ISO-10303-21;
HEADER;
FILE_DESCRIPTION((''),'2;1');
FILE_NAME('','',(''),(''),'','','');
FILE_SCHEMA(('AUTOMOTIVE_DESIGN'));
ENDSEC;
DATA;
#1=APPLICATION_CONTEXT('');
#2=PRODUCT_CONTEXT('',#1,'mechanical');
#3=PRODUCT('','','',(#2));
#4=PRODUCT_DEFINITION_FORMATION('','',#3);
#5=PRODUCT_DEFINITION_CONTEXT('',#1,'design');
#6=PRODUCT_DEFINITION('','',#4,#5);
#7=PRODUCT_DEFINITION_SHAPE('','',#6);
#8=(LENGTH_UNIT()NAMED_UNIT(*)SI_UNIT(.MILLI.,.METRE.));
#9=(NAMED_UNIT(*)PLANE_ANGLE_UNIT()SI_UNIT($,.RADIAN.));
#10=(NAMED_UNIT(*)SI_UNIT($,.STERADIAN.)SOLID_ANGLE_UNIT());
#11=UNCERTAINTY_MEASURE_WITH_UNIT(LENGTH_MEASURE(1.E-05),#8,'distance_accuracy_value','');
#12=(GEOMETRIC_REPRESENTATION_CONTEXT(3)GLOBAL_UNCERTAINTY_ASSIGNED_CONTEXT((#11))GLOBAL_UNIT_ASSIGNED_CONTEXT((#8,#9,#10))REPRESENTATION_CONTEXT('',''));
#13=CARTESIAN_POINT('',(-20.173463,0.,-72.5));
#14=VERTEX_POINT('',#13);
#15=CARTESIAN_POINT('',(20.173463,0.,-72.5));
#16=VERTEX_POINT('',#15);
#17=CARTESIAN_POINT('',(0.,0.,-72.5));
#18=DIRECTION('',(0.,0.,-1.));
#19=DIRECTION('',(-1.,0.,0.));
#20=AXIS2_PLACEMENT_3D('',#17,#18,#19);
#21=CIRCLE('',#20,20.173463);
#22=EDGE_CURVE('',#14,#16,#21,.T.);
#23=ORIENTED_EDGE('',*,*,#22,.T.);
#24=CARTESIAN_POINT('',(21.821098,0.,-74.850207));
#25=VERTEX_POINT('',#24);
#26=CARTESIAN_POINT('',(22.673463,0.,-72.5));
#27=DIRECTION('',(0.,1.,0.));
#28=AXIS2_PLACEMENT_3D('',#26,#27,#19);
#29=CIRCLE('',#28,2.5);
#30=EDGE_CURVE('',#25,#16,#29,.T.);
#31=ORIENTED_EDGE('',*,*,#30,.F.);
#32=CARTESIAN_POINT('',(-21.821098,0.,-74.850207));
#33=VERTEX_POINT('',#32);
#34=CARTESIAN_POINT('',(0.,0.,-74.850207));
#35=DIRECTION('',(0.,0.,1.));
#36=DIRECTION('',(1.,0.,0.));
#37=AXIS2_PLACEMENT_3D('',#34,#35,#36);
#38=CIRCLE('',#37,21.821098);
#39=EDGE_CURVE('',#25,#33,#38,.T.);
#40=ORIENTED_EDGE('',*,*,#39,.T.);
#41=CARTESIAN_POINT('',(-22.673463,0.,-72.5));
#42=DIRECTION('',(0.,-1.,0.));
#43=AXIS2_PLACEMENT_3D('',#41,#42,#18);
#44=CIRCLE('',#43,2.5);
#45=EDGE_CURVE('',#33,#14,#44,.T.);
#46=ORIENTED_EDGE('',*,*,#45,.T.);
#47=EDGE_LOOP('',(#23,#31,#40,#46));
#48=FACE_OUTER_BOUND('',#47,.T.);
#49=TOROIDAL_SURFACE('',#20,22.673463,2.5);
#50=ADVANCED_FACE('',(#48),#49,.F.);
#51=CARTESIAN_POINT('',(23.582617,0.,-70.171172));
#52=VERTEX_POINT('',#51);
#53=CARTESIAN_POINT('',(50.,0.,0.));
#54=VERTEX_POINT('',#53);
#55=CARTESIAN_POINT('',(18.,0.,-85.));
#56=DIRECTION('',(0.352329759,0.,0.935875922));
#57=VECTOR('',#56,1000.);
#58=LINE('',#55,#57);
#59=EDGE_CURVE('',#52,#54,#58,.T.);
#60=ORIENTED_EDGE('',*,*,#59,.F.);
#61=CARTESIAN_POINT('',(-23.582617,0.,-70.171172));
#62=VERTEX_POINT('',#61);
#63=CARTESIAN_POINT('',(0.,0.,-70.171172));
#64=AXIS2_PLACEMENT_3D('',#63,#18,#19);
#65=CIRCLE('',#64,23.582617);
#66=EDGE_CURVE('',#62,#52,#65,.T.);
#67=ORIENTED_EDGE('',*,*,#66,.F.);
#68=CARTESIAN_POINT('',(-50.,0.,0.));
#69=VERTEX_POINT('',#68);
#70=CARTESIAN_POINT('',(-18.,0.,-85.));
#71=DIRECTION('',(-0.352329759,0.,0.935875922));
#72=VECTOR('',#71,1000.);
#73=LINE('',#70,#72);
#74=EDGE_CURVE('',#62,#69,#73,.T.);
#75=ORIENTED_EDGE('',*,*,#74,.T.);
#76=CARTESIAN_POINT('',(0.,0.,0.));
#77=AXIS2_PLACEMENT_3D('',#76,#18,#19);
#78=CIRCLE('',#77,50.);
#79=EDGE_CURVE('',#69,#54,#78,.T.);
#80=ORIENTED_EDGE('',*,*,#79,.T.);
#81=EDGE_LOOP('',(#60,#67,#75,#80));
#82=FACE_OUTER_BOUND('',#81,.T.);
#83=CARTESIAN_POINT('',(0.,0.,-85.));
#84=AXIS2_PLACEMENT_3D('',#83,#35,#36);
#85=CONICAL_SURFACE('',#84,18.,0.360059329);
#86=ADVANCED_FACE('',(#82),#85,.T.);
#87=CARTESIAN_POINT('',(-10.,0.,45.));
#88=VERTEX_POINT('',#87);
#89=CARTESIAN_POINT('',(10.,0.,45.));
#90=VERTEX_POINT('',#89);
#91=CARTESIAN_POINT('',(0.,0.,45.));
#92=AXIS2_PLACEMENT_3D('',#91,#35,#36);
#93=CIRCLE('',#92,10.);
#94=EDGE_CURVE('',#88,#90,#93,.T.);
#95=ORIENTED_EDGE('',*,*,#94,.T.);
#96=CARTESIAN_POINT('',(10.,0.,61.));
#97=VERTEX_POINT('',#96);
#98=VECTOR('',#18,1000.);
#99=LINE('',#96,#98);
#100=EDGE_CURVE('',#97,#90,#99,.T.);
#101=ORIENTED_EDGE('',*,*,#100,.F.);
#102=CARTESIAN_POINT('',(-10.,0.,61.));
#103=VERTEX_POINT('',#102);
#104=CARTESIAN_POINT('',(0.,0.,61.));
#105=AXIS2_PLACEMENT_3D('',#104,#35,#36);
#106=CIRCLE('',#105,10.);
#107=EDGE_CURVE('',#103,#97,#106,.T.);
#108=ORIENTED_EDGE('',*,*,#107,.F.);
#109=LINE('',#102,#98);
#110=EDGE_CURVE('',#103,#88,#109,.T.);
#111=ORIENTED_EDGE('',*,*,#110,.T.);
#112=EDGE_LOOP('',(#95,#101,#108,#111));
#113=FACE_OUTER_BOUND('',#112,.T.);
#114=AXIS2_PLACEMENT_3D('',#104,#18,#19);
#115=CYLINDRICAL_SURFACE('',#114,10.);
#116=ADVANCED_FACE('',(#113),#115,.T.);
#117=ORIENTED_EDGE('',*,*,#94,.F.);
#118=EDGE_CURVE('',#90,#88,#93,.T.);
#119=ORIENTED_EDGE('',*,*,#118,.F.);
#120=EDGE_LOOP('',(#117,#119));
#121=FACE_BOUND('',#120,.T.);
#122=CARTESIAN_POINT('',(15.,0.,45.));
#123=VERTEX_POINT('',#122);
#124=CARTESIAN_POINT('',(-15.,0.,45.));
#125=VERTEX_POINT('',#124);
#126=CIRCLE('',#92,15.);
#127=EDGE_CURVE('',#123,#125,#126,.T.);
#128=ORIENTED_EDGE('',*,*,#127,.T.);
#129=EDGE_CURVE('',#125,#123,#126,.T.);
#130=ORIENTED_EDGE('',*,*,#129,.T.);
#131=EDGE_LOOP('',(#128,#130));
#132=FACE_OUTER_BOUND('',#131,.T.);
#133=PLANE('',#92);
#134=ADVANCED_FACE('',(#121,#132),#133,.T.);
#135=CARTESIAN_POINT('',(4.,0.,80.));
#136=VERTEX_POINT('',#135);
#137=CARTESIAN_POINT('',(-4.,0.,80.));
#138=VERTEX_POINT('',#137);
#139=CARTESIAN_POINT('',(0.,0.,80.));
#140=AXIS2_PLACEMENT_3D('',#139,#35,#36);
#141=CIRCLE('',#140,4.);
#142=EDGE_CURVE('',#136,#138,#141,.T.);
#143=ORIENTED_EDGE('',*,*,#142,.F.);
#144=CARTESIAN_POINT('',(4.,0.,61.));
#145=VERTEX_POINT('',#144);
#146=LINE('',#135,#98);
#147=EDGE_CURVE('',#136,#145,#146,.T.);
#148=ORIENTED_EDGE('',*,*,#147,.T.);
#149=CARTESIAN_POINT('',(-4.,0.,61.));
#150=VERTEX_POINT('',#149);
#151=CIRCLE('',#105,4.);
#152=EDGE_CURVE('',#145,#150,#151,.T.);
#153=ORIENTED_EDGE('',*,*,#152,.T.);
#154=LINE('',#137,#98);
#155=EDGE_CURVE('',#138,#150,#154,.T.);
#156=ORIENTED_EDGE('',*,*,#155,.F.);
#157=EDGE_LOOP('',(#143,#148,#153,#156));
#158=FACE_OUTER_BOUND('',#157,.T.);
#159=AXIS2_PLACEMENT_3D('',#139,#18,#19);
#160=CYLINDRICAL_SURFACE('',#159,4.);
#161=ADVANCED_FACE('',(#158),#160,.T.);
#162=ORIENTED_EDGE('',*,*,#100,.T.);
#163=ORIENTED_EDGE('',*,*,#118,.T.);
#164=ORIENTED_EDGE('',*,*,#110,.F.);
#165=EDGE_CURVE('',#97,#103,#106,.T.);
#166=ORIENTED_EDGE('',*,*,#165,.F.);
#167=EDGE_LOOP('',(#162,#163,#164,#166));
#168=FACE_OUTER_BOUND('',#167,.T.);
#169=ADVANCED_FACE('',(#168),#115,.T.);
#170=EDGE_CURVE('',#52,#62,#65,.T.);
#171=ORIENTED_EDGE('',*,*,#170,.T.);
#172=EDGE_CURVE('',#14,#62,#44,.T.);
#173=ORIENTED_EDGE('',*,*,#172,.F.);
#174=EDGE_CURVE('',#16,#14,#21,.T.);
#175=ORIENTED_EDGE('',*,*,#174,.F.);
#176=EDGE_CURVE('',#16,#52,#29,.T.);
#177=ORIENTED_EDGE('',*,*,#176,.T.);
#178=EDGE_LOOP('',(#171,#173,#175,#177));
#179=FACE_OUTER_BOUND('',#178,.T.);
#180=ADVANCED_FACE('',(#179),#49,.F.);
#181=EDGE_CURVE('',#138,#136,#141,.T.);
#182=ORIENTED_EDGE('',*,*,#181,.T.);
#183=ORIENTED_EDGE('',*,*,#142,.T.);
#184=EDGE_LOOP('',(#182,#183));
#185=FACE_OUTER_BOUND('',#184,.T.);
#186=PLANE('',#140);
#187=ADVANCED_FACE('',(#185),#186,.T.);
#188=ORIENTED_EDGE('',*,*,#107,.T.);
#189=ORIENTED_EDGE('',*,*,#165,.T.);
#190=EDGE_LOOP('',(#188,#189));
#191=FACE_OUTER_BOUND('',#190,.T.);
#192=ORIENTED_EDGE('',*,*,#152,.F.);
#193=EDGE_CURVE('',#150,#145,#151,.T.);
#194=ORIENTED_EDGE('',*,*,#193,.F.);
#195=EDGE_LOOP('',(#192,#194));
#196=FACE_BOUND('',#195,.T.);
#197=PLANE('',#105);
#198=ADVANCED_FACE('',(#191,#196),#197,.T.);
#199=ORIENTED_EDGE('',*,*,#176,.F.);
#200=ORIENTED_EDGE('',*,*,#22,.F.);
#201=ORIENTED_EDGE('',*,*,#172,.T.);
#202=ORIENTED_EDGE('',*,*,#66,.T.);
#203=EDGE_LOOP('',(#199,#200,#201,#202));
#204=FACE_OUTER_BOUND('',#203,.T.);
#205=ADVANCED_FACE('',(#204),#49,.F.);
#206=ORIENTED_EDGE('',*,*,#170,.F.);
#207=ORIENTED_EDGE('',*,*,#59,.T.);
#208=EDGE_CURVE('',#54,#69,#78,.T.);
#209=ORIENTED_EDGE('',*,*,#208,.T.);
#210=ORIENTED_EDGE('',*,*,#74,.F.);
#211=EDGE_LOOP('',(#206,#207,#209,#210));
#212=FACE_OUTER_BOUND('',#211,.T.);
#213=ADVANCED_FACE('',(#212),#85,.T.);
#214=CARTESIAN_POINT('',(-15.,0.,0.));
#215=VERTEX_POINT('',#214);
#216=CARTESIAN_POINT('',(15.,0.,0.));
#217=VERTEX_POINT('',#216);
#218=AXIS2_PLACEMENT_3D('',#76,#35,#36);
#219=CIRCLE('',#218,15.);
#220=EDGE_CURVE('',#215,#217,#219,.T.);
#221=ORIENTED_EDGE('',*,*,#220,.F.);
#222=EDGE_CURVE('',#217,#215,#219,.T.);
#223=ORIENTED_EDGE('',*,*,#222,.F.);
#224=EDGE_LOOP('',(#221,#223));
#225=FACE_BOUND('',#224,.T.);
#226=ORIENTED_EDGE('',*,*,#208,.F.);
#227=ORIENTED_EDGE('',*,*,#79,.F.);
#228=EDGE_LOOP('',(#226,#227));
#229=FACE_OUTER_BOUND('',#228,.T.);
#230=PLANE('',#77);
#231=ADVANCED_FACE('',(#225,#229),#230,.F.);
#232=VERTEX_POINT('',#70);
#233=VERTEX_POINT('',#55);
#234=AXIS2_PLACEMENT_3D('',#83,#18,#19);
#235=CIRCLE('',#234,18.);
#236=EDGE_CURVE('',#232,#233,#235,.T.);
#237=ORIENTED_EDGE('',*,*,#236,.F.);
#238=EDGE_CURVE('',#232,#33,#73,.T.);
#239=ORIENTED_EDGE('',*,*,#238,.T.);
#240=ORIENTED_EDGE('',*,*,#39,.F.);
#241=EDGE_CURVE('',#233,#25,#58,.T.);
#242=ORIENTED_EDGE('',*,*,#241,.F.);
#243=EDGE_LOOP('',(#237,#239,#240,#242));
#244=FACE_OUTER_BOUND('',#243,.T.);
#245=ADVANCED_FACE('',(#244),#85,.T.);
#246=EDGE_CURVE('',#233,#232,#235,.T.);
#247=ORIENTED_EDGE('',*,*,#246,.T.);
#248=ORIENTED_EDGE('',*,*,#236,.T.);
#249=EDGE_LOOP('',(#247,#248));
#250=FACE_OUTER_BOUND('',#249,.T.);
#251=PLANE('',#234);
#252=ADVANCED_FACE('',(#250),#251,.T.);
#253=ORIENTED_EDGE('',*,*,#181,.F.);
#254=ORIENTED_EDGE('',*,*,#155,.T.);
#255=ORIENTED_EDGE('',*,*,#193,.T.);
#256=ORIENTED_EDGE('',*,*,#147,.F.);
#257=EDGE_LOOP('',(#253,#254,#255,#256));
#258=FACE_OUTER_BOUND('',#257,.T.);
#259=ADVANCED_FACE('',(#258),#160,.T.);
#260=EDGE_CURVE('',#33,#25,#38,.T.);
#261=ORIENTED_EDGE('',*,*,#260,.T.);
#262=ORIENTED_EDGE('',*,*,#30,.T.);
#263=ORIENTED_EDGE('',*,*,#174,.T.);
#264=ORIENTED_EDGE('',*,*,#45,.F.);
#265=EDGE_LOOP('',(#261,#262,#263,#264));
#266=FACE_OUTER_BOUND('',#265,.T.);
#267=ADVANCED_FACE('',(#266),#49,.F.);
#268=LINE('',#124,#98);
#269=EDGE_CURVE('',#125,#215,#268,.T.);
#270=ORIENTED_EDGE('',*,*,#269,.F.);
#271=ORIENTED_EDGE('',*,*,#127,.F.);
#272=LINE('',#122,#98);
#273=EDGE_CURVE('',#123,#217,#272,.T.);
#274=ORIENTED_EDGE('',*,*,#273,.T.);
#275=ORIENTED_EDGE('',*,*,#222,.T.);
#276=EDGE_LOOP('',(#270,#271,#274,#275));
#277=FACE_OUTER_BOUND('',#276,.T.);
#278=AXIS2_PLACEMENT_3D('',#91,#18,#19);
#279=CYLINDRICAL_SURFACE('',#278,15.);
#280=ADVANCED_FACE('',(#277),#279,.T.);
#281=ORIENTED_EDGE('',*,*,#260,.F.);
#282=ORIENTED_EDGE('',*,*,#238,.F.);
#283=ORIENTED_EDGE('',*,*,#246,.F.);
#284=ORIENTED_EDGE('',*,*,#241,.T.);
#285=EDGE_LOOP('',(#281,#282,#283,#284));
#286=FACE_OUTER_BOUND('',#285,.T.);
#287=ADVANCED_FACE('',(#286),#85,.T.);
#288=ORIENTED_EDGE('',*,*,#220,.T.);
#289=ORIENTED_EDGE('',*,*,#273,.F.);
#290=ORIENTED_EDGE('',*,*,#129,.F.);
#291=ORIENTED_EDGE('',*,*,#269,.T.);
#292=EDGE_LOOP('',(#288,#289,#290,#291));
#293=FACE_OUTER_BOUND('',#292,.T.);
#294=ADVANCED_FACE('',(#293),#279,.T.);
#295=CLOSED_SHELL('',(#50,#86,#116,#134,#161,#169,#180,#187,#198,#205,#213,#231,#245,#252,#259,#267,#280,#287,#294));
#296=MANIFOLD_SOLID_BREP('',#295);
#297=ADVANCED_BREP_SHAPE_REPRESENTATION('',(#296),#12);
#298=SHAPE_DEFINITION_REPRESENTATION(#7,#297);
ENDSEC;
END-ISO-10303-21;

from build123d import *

# Parameters (mm, degrees)
SHAFT_BASE_30_SKETCH_R     = 15
SHAFT_BASE_30_DEPTH        = 45
SHAFT_STEP_2_SKETCH_R      = 10
SHAFT_STEP_2_DEPTH         = 16
SHAFT_TIP_SKETCH_R         = 4
SHAFT_TIP_DEPTH            = 19
CONE_SMALL_END_36_SKETCH_R = 18
CONE_BASE_100_SKETCH_R     = 50
GROOVE_SWEEP_CUT_PROFILE_R = 2.5


with BuildPart() as part:
    # Shaft Base Ø30 Sketch → Shaft Base Ø30 (new body)
    with BuildSketch(Plane.XY):
        with Locations(Location((0, 0, 0), (0, 0, 180))):
            Circle(SHAFT_BASE_30_SKETCH_R)
    extrude(amount=SHAFT_BASE_30_DEPTH)

    # Shaft Step 2 Sketch → Shaft Step 2 (add)
    with BuildSketch(Plane.XY.offset(45)):
        Circle(SHAFT_STEP_2_SKETCH_R)
    extrude(amount=SHAFT_STEP_2_DEPTH)

    # Shaft Tip Sketch → Shaft Tip (add)
    with BuildSketch(Plane.XY.offset(61)):
        Circle(SHAFT_TIP_SKETCH_R)
    extrude(amount=SHAFT_TIP_DEPTH)

    # Cone Small End Ø36 Sketch → Conical Body section 0
    with BuildSketch(Plane(origin=(0, 0, -85), x_dir=(-1, 0, 0), z_dir=(0, 0, -1))):
        Circle(CONE_SMALL_END_36_SKETCH_R)
    # Cone Base Ø100 Sketch → Conical Body section 1
    with BuildSketch(Plane(origin=(0, 0, 0), x_dir=(-1, 0, 0), z_dir=(0, 0, -1))):
        Circle(CONE_BASE_100_SKETCH_R)
    loft()

    # Groove Sweep Cut: sweep along a path in Groove Path
    with BuildLine(Plane(origin=(0, 0, -72.5), x_dir=(-1, 0, 0), z_dir=(0, 0, -1))) as groove_sweep_cut_path:
        CenterArc((0, 0), 22.673462662, 0, 360)
    # Groove Sweep Cut profile (on start of the path) → Groove Sweep Cut (sweep, cut)
    with BuildSketch(Plane(origin=(-22.673462662, 0, -72.5), x_dir=(0, 0, 1), z_dir=(0, 1, 0))):
        Circle(GROOVE_SWEEP_CUT_PROFILE_R)
    sweep(path=groove_sweep_cut_path.line, mode=Mode.SUBTRACT)


solid = part.part
